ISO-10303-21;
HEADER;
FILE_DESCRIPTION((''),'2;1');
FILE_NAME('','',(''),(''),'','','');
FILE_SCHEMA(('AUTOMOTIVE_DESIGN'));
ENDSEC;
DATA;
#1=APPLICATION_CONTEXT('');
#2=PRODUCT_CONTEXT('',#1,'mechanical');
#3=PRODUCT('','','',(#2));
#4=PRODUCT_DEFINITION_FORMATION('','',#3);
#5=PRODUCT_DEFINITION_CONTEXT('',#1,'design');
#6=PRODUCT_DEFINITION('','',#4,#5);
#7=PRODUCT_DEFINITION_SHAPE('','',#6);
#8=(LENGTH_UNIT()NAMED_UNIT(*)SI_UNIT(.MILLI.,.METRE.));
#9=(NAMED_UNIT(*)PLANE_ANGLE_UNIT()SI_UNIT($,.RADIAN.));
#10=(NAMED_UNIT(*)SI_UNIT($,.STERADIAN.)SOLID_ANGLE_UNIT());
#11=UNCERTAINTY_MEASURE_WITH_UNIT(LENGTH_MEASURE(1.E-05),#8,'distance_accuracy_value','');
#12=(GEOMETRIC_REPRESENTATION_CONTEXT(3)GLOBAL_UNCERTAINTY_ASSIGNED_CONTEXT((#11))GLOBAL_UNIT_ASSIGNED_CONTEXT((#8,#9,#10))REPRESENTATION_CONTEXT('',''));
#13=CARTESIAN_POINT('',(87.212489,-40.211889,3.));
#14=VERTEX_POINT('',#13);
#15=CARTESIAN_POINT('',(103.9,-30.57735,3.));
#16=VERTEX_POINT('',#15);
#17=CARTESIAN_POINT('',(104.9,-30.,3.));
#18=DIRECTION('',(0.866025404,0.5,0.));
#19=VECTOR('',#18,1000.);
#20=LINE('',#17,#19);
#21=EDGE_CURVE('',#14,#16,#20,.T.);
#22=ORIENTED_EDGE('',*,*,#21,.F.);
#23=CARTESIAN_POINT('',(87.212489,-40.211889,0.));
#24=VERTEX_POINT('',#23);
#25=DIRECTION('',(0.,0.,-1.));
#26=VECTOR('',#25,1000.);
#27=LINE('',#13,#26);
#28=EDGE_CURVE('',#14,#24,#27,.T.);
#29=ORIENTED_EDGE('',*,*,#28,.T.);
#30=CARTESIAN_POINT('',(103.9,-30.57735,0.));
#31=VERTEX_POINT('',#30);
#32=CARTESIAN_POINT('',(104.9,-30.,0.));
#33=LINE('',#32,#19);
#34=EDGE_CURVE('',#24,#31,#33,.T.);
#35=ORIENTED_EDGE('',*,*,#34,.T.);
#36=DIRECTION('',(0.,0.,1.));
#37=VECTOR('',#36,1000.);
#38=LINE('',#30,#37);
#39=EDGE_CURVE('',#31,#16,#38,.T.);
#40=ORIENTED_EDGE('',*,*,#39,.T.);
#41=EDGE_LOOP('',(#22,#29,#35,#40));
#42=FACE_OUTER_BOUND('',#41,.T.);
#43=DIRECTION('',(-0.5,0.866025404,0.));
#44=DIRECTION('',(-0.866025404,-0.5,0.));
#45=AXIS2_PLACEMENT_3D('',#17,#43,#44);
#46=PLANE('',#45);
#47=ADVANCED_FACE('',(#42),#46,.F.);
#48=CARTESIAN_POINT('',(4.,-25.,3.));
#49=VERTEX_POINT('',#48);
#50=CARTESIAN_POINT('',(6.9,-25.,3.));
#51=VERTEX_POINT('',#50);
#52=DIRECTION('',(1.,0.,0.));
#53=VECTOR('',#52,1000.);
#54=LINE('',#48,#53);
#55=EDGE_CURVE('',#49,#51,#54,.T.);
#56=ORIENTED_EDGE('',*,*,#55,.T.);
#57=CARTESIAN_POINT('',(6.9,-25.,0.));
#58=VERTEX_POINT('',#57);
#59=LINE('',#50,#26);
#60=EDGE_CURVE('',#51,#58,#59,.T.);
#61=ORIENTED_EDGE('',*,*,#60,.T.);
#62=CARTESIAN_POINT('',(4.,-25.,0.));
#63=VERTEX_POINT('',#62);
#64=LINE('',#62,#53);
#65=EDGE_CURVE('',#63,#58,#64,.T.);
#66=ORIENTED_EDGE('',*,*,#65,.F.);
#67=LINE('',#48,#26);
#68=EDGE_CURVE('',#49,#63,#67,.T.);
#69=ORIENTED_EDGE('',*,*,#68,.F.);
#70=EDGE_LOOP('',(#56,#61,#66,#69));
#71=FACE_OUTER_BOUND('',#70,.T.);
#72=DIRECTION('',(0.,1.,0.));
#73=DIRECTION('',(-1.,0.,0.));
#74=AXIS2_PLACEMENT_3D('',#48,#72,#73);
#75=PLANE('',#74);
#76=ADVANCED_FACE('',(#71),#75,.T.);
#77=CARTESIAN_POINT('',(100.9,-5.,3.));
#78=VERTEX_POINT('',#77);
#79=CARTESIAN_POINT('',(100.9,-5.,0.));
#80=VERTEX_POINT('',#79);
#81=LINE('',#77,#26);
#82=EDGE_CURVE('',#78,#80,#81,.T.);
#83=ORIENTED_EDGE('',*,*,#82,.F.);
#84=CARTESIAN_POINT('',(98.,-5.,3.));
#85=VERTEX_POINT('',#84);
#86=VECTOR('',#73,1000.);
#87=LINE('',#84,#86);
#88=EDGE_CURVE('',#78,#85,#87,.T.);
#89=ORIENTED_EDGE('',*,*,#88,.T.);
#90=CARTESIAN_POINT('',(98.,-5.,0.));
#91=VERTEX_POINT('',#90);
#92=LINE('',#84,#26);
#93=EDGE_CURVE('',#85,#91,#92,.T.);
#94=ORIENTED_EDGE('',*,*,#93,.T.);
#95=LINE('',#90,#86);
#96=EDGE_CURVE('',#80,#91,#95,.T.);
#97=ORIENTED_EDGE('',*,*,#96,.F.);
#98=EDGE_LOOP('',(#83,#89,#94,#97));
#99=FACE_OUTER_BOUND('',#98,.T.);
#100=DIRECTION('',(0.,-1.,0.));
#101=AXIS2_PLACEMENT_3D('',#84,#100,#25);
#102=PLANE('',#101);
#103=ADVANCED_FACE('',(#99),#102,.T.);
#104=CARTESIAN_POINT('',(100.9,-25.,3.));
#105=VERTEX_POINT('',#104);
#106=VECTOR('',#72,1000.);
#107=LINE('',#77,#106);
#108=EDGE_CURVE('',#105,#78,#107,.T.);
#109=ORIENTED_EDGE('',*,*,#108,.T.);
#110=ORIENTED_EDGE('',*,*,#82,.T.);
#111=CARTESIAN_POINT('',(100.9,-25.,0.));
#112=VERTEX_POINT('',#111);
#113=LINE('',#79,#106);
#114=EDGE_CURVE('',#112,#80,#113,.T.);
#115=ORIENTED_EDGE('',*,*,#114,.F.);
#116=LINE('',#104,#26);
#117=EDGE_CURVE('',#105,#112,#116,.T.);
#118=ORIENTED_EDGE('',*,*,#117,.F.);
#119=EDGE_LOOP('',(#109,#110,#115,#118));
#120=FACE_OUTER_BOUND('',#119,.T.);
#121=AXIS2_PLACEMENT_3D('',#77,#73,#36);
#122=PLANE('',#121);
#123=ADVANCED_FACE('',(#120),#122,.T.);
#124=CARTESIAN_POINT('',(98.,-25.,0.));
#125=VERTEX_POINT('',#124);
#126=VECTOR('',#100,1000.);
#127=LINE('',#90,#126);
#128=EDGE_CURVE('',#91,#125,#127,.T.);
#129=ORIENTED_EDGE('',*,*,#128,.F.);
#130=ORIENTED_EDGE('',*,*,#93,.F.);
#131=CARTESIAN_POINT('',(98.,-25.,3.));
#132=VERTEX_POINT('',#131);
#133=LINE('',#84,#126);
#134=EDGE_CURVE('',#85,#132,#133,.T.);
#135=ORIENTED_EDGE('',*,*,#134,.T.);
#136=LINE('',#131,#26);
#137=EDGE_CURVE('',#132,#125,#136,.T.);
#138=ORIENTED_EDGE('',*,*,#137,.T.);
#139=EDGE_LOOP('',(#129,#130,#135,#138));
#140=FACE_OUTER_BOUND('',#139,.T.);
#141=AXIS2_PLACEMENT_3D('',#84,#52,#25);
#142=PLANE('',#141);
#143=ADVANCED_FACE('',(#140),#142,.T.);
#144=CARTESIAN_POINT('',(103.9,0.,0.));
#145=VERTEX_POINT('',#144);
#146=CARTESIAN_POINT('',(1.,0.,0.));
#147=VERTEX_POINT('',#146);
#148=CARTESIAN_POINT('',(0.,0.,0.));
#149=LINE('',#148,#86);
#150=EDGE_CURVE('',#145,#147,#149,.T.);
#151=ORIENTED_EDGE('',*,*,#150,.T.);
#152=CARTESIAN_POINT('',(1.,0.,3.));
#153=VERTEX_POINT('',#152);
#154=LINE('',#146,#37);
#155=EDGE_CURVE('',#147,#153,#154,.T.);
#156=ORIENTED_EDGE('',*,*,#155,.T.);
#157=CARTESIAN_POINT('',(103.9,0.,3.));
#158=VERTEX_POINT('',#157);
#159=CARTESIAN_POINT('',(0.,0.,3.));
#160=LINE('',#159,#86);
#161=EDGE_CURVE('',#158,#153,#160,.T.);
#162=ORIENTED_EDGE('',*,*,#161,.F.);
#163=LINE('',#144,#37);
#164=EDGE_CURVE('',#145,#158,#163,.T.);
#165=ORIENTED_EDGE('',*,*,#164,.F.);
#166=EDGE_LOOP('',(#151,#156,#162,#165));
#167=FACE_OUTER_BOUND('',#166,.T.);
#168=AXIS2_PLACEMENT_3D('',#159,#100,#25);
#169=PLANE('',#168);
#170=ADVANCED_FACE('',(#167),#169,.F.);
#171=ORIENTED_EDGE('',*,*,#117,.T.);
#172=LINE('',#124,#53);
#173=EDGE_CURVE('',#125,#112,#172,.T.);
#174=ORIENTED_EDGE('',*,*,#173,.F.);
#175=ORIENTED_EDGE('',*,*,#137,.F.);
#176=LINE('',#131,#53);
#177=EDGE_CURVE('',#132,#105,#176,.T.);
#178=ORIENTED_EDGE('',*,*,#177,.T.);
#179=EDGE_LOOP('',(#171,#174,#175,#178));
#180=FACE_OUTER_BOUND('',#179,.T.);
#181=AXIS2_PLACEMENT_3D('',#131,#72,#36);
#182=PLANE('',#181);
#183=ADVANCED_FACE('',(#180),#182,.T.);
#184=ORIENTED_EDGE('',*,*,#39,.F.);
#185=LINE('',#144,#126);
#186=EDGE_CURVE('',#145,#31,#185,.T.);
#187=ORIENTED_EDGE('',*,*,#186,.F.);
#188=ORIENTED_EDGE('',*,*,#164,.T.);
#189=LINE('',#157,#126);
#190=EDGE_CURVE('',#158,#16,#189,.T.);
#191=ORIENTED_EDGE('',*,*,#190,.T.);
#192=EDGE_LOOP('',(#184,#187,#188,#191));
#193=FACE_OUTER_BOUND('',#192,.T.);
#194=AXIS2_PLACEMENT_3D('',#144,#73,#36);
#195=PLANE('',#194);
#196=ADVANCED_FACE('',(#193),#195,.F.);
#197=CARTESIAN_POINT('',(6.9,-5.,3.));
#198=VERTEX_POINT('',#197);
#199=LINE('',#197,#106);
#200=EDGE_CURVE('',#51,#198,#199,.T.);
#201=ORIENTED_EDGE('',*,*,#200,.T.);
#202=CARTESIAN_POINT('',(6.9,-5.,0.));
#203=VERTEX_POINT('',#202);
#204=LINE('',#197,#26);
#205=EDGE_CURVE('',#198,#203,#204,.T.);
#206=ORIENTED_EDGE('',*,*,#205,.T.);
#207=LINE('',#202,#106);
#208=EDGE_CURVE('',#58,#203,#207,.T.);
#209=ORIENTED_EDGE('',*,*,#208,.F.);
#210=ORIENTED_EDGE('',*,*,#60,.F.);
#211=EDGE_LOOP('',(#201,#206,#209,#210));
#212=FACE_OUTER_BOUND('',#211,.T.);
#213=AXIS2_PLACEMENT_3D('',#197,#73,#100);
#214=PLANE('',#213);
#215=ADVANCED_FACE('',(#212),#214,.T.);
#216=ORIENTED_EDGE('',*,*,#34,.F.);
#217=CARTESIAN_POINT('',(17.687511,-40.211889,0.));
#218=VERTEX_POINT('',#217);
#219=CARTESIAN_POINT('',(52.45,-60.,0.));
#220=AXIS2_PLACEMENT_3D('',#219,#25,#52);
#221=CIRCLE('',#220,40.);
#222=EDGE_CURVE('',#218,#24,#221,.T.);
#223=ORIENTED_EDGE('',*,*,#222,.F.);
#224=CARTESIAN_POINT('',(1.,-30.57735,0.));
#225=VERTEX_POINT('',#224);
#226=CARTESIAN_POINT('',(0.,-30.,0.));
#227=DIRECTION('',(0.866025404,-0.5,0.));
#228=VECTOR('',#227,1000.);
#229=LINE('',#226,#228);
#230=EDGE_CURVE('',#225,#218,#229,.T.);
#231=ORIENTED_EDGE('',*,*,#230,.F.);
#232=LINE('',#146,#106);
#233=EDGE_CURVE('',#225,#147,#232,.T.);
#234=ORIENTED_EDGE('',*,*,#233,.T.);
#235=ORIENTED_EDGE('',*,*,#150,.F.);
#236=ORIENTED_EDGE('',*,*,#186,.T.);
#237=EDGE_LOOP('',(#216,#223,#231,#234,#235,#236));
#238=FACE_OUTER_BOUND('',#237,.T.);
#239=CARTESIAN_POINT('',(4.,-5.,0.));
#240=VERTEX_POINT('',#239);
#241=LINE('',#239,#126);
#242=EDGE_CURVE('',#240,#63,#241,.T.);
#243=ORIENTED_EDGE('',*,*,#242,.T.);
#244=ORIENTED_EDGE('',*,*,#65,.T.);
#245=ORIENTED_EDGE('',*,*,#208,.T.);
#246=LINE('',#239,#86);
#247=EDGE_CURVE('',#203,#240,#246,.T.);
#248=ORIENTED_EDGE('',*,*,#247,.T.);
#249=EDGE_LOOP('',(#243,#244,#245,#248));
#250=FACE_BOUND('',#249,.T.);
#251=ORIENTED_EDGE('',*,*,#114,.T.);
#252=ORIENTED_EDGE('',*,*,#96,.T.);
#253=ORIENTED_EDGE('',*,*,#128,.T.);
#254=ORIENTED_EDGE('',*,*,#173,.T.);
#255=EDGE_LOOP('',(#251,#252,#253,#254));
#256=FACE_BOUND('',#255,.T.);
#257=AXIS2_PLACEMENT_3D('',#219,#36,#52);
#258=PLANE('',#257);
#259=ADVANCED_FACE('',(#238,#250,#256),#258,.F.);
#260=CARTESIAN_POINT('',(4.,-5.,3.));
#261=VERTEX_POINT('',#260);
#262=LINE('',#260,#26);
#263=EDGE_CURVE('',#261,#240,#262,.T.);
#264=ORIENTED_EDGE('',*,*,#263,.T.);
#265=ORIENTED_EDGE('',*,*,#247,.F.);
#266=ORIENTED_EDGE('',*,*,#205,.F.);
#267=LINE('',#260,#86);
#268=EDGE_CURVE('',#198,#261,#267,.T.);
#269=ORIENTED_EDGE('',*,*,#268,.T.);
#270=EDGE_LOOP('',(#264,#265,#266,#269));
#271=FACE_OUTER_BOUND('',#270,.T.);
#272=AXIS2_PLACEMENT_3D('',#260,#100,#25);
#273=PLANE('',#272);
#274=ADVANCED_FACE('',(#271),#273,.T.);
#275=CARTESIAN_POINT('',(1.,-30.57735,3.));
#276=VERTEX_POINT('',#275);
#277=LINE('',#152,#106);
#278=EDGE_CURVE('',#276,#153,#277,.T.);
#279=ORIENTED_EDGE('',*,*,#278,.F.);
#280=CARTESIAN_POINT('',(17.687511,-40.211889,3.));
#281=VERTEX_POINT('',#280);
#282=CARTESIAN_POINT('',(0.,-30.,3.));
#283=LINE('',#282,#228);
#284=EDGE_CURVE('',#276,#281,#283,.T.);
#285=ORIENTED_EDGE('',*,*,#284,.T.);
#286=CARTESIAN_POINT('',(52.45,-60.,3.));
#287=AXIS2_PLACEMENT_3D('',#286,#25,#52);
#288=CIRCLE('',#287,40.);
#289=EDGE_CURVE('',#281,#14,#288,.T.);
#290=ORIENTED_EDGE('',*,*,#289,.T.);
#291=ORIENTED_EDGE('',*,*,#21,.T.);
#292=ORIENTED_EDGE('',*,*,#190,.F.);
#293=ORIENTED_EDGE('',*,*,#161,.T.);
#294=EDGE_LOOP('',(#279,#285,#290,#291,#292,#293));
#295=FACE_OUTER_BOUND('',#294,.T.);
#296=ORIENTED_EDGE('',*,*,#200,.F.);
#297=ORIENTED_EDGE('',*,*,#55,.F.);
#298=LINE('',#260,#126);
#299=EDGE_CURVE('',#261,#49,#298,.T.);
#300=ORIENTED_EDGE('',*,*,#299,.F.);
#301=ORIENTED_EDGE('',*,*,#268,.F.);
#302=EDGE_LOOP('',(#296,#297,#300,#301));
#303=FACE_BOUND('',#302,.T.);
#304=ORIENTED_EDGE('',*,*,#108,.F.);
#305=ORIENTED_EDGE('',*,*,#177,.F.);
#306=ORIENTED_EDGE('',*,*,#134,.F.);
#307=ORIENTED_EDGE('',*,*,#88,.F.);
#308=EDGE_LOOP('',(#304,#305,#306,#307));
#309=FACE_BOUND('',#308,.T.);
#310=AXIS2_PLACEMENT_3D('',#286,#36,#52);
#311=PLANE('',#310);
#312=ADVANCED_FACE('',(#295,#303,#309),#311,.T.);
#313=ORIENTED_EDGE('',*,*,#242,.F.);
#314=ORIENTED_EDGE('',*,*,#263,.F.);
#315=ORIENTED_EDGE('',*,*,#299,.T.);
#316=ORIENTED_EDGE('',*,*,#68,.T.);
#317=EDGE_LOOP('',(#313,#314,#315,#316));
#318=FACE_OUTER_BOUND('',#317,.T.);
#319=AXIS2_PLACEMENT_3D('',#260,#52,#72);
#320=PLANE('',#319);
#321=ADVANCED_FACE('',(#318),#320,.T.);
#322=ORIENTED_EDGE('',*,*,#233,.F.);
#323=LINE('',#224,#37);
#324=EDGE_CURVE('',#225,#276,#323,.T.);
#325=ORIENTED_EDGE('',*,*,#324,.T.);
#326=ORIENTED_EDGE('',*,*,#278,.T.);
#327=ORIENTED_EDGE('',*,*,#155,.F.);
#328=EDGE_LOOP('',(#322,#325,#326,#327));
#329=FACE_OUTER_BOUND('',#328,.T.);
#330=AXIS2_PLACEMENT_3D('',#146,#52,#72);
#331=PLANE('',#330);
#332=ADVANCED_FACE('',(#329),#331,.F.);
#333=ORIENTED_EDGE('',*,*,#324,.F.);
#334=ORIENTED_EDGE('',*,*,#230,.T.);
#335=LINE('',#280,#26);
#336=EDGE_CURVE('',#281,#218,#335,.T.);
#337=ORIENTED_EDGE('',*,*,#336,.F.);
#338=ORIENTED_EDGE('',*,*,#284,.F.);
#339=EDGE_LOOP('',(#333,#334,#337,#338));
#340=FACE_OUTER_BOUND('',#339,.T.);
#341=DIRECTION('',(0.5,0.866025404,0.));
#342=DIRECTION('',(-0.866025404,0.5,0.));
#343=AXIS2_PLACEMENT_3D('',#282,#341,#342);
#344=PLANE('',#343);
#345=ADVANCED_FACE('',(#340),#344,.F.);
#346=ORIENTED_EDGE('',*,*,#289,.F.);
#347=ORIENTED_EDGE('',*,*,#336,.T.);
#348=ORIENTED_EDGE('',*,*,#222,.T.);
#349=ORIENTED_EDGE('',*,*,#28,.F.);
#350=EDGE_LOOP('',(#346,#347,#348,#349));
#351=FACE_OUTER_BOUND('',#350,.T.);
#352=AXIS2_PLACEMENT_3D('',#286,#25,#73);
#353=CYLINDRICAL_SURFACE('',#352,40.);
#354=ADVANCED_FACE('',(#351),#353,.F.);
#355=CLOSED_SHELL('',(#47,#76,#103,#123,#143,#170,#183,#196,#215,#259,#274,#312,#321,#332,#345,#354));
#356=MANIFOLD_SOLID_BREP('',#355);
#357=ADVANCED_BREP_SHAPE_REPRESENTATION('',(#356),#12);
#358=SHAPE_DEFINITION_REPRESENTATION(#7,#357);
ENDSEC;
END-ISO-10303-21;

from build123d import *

# Parameters (mm, degrees)
SKETCH1_W           = 2.9
SKETCH1_H           = 20
BOSS_EXTRUDE1_DEPTH = 3
CUT_EXTRUDE1_DEPTH  = 113.383299562


with BuildPart() as part:
    # Sketch1 → Boss-Extrude1 (new body)
    with BuildSketch(Plane.XY):
        with BuildLine():
            Line((0, 0), (104.9, 0))
            Line((104.9, 0), (104.9, -30))
            Line((104.9, -30), (87.212489335, -40.211889044))
            ThreePointArc((87.212489335, -40.211889044), (52.45, -20), (17.687510665, -40.211889044))
            Line((17.687510665, -40.211889044), (0, -30))
            Line((0, -30), (0, 0))
        make_face()
        with Locations((99.45, -15)):
            Rectangle(SKETCH1_W, SKETCH1_H, mode=Mode.SUBTRACT)
        with Locations((5.45, -15)):
            Rectangle(SKETCH1_W, SKETCH1_H, mode=Mode.SUBTRACT)
    extrude(amount=BOSS_EXTRUDE1_DEPTH)

    # Sketch2 → Cut-Extrude1 (cut, through all)
    with BuildSketch(Plane.XY.offset(3)):
        Polygon((1, 0), (1, -30.577350269), (0, -30), (0, 0), align=None)
        Polygon((103.9, 0), (103.9, -30.577350269), (104.9, -30), (104.9, 0), align=None)
    extrude(amount=-CUT_EXTRUDE1_DEPTH, mode=Mode.SUBTRACT)


solid = part.part
